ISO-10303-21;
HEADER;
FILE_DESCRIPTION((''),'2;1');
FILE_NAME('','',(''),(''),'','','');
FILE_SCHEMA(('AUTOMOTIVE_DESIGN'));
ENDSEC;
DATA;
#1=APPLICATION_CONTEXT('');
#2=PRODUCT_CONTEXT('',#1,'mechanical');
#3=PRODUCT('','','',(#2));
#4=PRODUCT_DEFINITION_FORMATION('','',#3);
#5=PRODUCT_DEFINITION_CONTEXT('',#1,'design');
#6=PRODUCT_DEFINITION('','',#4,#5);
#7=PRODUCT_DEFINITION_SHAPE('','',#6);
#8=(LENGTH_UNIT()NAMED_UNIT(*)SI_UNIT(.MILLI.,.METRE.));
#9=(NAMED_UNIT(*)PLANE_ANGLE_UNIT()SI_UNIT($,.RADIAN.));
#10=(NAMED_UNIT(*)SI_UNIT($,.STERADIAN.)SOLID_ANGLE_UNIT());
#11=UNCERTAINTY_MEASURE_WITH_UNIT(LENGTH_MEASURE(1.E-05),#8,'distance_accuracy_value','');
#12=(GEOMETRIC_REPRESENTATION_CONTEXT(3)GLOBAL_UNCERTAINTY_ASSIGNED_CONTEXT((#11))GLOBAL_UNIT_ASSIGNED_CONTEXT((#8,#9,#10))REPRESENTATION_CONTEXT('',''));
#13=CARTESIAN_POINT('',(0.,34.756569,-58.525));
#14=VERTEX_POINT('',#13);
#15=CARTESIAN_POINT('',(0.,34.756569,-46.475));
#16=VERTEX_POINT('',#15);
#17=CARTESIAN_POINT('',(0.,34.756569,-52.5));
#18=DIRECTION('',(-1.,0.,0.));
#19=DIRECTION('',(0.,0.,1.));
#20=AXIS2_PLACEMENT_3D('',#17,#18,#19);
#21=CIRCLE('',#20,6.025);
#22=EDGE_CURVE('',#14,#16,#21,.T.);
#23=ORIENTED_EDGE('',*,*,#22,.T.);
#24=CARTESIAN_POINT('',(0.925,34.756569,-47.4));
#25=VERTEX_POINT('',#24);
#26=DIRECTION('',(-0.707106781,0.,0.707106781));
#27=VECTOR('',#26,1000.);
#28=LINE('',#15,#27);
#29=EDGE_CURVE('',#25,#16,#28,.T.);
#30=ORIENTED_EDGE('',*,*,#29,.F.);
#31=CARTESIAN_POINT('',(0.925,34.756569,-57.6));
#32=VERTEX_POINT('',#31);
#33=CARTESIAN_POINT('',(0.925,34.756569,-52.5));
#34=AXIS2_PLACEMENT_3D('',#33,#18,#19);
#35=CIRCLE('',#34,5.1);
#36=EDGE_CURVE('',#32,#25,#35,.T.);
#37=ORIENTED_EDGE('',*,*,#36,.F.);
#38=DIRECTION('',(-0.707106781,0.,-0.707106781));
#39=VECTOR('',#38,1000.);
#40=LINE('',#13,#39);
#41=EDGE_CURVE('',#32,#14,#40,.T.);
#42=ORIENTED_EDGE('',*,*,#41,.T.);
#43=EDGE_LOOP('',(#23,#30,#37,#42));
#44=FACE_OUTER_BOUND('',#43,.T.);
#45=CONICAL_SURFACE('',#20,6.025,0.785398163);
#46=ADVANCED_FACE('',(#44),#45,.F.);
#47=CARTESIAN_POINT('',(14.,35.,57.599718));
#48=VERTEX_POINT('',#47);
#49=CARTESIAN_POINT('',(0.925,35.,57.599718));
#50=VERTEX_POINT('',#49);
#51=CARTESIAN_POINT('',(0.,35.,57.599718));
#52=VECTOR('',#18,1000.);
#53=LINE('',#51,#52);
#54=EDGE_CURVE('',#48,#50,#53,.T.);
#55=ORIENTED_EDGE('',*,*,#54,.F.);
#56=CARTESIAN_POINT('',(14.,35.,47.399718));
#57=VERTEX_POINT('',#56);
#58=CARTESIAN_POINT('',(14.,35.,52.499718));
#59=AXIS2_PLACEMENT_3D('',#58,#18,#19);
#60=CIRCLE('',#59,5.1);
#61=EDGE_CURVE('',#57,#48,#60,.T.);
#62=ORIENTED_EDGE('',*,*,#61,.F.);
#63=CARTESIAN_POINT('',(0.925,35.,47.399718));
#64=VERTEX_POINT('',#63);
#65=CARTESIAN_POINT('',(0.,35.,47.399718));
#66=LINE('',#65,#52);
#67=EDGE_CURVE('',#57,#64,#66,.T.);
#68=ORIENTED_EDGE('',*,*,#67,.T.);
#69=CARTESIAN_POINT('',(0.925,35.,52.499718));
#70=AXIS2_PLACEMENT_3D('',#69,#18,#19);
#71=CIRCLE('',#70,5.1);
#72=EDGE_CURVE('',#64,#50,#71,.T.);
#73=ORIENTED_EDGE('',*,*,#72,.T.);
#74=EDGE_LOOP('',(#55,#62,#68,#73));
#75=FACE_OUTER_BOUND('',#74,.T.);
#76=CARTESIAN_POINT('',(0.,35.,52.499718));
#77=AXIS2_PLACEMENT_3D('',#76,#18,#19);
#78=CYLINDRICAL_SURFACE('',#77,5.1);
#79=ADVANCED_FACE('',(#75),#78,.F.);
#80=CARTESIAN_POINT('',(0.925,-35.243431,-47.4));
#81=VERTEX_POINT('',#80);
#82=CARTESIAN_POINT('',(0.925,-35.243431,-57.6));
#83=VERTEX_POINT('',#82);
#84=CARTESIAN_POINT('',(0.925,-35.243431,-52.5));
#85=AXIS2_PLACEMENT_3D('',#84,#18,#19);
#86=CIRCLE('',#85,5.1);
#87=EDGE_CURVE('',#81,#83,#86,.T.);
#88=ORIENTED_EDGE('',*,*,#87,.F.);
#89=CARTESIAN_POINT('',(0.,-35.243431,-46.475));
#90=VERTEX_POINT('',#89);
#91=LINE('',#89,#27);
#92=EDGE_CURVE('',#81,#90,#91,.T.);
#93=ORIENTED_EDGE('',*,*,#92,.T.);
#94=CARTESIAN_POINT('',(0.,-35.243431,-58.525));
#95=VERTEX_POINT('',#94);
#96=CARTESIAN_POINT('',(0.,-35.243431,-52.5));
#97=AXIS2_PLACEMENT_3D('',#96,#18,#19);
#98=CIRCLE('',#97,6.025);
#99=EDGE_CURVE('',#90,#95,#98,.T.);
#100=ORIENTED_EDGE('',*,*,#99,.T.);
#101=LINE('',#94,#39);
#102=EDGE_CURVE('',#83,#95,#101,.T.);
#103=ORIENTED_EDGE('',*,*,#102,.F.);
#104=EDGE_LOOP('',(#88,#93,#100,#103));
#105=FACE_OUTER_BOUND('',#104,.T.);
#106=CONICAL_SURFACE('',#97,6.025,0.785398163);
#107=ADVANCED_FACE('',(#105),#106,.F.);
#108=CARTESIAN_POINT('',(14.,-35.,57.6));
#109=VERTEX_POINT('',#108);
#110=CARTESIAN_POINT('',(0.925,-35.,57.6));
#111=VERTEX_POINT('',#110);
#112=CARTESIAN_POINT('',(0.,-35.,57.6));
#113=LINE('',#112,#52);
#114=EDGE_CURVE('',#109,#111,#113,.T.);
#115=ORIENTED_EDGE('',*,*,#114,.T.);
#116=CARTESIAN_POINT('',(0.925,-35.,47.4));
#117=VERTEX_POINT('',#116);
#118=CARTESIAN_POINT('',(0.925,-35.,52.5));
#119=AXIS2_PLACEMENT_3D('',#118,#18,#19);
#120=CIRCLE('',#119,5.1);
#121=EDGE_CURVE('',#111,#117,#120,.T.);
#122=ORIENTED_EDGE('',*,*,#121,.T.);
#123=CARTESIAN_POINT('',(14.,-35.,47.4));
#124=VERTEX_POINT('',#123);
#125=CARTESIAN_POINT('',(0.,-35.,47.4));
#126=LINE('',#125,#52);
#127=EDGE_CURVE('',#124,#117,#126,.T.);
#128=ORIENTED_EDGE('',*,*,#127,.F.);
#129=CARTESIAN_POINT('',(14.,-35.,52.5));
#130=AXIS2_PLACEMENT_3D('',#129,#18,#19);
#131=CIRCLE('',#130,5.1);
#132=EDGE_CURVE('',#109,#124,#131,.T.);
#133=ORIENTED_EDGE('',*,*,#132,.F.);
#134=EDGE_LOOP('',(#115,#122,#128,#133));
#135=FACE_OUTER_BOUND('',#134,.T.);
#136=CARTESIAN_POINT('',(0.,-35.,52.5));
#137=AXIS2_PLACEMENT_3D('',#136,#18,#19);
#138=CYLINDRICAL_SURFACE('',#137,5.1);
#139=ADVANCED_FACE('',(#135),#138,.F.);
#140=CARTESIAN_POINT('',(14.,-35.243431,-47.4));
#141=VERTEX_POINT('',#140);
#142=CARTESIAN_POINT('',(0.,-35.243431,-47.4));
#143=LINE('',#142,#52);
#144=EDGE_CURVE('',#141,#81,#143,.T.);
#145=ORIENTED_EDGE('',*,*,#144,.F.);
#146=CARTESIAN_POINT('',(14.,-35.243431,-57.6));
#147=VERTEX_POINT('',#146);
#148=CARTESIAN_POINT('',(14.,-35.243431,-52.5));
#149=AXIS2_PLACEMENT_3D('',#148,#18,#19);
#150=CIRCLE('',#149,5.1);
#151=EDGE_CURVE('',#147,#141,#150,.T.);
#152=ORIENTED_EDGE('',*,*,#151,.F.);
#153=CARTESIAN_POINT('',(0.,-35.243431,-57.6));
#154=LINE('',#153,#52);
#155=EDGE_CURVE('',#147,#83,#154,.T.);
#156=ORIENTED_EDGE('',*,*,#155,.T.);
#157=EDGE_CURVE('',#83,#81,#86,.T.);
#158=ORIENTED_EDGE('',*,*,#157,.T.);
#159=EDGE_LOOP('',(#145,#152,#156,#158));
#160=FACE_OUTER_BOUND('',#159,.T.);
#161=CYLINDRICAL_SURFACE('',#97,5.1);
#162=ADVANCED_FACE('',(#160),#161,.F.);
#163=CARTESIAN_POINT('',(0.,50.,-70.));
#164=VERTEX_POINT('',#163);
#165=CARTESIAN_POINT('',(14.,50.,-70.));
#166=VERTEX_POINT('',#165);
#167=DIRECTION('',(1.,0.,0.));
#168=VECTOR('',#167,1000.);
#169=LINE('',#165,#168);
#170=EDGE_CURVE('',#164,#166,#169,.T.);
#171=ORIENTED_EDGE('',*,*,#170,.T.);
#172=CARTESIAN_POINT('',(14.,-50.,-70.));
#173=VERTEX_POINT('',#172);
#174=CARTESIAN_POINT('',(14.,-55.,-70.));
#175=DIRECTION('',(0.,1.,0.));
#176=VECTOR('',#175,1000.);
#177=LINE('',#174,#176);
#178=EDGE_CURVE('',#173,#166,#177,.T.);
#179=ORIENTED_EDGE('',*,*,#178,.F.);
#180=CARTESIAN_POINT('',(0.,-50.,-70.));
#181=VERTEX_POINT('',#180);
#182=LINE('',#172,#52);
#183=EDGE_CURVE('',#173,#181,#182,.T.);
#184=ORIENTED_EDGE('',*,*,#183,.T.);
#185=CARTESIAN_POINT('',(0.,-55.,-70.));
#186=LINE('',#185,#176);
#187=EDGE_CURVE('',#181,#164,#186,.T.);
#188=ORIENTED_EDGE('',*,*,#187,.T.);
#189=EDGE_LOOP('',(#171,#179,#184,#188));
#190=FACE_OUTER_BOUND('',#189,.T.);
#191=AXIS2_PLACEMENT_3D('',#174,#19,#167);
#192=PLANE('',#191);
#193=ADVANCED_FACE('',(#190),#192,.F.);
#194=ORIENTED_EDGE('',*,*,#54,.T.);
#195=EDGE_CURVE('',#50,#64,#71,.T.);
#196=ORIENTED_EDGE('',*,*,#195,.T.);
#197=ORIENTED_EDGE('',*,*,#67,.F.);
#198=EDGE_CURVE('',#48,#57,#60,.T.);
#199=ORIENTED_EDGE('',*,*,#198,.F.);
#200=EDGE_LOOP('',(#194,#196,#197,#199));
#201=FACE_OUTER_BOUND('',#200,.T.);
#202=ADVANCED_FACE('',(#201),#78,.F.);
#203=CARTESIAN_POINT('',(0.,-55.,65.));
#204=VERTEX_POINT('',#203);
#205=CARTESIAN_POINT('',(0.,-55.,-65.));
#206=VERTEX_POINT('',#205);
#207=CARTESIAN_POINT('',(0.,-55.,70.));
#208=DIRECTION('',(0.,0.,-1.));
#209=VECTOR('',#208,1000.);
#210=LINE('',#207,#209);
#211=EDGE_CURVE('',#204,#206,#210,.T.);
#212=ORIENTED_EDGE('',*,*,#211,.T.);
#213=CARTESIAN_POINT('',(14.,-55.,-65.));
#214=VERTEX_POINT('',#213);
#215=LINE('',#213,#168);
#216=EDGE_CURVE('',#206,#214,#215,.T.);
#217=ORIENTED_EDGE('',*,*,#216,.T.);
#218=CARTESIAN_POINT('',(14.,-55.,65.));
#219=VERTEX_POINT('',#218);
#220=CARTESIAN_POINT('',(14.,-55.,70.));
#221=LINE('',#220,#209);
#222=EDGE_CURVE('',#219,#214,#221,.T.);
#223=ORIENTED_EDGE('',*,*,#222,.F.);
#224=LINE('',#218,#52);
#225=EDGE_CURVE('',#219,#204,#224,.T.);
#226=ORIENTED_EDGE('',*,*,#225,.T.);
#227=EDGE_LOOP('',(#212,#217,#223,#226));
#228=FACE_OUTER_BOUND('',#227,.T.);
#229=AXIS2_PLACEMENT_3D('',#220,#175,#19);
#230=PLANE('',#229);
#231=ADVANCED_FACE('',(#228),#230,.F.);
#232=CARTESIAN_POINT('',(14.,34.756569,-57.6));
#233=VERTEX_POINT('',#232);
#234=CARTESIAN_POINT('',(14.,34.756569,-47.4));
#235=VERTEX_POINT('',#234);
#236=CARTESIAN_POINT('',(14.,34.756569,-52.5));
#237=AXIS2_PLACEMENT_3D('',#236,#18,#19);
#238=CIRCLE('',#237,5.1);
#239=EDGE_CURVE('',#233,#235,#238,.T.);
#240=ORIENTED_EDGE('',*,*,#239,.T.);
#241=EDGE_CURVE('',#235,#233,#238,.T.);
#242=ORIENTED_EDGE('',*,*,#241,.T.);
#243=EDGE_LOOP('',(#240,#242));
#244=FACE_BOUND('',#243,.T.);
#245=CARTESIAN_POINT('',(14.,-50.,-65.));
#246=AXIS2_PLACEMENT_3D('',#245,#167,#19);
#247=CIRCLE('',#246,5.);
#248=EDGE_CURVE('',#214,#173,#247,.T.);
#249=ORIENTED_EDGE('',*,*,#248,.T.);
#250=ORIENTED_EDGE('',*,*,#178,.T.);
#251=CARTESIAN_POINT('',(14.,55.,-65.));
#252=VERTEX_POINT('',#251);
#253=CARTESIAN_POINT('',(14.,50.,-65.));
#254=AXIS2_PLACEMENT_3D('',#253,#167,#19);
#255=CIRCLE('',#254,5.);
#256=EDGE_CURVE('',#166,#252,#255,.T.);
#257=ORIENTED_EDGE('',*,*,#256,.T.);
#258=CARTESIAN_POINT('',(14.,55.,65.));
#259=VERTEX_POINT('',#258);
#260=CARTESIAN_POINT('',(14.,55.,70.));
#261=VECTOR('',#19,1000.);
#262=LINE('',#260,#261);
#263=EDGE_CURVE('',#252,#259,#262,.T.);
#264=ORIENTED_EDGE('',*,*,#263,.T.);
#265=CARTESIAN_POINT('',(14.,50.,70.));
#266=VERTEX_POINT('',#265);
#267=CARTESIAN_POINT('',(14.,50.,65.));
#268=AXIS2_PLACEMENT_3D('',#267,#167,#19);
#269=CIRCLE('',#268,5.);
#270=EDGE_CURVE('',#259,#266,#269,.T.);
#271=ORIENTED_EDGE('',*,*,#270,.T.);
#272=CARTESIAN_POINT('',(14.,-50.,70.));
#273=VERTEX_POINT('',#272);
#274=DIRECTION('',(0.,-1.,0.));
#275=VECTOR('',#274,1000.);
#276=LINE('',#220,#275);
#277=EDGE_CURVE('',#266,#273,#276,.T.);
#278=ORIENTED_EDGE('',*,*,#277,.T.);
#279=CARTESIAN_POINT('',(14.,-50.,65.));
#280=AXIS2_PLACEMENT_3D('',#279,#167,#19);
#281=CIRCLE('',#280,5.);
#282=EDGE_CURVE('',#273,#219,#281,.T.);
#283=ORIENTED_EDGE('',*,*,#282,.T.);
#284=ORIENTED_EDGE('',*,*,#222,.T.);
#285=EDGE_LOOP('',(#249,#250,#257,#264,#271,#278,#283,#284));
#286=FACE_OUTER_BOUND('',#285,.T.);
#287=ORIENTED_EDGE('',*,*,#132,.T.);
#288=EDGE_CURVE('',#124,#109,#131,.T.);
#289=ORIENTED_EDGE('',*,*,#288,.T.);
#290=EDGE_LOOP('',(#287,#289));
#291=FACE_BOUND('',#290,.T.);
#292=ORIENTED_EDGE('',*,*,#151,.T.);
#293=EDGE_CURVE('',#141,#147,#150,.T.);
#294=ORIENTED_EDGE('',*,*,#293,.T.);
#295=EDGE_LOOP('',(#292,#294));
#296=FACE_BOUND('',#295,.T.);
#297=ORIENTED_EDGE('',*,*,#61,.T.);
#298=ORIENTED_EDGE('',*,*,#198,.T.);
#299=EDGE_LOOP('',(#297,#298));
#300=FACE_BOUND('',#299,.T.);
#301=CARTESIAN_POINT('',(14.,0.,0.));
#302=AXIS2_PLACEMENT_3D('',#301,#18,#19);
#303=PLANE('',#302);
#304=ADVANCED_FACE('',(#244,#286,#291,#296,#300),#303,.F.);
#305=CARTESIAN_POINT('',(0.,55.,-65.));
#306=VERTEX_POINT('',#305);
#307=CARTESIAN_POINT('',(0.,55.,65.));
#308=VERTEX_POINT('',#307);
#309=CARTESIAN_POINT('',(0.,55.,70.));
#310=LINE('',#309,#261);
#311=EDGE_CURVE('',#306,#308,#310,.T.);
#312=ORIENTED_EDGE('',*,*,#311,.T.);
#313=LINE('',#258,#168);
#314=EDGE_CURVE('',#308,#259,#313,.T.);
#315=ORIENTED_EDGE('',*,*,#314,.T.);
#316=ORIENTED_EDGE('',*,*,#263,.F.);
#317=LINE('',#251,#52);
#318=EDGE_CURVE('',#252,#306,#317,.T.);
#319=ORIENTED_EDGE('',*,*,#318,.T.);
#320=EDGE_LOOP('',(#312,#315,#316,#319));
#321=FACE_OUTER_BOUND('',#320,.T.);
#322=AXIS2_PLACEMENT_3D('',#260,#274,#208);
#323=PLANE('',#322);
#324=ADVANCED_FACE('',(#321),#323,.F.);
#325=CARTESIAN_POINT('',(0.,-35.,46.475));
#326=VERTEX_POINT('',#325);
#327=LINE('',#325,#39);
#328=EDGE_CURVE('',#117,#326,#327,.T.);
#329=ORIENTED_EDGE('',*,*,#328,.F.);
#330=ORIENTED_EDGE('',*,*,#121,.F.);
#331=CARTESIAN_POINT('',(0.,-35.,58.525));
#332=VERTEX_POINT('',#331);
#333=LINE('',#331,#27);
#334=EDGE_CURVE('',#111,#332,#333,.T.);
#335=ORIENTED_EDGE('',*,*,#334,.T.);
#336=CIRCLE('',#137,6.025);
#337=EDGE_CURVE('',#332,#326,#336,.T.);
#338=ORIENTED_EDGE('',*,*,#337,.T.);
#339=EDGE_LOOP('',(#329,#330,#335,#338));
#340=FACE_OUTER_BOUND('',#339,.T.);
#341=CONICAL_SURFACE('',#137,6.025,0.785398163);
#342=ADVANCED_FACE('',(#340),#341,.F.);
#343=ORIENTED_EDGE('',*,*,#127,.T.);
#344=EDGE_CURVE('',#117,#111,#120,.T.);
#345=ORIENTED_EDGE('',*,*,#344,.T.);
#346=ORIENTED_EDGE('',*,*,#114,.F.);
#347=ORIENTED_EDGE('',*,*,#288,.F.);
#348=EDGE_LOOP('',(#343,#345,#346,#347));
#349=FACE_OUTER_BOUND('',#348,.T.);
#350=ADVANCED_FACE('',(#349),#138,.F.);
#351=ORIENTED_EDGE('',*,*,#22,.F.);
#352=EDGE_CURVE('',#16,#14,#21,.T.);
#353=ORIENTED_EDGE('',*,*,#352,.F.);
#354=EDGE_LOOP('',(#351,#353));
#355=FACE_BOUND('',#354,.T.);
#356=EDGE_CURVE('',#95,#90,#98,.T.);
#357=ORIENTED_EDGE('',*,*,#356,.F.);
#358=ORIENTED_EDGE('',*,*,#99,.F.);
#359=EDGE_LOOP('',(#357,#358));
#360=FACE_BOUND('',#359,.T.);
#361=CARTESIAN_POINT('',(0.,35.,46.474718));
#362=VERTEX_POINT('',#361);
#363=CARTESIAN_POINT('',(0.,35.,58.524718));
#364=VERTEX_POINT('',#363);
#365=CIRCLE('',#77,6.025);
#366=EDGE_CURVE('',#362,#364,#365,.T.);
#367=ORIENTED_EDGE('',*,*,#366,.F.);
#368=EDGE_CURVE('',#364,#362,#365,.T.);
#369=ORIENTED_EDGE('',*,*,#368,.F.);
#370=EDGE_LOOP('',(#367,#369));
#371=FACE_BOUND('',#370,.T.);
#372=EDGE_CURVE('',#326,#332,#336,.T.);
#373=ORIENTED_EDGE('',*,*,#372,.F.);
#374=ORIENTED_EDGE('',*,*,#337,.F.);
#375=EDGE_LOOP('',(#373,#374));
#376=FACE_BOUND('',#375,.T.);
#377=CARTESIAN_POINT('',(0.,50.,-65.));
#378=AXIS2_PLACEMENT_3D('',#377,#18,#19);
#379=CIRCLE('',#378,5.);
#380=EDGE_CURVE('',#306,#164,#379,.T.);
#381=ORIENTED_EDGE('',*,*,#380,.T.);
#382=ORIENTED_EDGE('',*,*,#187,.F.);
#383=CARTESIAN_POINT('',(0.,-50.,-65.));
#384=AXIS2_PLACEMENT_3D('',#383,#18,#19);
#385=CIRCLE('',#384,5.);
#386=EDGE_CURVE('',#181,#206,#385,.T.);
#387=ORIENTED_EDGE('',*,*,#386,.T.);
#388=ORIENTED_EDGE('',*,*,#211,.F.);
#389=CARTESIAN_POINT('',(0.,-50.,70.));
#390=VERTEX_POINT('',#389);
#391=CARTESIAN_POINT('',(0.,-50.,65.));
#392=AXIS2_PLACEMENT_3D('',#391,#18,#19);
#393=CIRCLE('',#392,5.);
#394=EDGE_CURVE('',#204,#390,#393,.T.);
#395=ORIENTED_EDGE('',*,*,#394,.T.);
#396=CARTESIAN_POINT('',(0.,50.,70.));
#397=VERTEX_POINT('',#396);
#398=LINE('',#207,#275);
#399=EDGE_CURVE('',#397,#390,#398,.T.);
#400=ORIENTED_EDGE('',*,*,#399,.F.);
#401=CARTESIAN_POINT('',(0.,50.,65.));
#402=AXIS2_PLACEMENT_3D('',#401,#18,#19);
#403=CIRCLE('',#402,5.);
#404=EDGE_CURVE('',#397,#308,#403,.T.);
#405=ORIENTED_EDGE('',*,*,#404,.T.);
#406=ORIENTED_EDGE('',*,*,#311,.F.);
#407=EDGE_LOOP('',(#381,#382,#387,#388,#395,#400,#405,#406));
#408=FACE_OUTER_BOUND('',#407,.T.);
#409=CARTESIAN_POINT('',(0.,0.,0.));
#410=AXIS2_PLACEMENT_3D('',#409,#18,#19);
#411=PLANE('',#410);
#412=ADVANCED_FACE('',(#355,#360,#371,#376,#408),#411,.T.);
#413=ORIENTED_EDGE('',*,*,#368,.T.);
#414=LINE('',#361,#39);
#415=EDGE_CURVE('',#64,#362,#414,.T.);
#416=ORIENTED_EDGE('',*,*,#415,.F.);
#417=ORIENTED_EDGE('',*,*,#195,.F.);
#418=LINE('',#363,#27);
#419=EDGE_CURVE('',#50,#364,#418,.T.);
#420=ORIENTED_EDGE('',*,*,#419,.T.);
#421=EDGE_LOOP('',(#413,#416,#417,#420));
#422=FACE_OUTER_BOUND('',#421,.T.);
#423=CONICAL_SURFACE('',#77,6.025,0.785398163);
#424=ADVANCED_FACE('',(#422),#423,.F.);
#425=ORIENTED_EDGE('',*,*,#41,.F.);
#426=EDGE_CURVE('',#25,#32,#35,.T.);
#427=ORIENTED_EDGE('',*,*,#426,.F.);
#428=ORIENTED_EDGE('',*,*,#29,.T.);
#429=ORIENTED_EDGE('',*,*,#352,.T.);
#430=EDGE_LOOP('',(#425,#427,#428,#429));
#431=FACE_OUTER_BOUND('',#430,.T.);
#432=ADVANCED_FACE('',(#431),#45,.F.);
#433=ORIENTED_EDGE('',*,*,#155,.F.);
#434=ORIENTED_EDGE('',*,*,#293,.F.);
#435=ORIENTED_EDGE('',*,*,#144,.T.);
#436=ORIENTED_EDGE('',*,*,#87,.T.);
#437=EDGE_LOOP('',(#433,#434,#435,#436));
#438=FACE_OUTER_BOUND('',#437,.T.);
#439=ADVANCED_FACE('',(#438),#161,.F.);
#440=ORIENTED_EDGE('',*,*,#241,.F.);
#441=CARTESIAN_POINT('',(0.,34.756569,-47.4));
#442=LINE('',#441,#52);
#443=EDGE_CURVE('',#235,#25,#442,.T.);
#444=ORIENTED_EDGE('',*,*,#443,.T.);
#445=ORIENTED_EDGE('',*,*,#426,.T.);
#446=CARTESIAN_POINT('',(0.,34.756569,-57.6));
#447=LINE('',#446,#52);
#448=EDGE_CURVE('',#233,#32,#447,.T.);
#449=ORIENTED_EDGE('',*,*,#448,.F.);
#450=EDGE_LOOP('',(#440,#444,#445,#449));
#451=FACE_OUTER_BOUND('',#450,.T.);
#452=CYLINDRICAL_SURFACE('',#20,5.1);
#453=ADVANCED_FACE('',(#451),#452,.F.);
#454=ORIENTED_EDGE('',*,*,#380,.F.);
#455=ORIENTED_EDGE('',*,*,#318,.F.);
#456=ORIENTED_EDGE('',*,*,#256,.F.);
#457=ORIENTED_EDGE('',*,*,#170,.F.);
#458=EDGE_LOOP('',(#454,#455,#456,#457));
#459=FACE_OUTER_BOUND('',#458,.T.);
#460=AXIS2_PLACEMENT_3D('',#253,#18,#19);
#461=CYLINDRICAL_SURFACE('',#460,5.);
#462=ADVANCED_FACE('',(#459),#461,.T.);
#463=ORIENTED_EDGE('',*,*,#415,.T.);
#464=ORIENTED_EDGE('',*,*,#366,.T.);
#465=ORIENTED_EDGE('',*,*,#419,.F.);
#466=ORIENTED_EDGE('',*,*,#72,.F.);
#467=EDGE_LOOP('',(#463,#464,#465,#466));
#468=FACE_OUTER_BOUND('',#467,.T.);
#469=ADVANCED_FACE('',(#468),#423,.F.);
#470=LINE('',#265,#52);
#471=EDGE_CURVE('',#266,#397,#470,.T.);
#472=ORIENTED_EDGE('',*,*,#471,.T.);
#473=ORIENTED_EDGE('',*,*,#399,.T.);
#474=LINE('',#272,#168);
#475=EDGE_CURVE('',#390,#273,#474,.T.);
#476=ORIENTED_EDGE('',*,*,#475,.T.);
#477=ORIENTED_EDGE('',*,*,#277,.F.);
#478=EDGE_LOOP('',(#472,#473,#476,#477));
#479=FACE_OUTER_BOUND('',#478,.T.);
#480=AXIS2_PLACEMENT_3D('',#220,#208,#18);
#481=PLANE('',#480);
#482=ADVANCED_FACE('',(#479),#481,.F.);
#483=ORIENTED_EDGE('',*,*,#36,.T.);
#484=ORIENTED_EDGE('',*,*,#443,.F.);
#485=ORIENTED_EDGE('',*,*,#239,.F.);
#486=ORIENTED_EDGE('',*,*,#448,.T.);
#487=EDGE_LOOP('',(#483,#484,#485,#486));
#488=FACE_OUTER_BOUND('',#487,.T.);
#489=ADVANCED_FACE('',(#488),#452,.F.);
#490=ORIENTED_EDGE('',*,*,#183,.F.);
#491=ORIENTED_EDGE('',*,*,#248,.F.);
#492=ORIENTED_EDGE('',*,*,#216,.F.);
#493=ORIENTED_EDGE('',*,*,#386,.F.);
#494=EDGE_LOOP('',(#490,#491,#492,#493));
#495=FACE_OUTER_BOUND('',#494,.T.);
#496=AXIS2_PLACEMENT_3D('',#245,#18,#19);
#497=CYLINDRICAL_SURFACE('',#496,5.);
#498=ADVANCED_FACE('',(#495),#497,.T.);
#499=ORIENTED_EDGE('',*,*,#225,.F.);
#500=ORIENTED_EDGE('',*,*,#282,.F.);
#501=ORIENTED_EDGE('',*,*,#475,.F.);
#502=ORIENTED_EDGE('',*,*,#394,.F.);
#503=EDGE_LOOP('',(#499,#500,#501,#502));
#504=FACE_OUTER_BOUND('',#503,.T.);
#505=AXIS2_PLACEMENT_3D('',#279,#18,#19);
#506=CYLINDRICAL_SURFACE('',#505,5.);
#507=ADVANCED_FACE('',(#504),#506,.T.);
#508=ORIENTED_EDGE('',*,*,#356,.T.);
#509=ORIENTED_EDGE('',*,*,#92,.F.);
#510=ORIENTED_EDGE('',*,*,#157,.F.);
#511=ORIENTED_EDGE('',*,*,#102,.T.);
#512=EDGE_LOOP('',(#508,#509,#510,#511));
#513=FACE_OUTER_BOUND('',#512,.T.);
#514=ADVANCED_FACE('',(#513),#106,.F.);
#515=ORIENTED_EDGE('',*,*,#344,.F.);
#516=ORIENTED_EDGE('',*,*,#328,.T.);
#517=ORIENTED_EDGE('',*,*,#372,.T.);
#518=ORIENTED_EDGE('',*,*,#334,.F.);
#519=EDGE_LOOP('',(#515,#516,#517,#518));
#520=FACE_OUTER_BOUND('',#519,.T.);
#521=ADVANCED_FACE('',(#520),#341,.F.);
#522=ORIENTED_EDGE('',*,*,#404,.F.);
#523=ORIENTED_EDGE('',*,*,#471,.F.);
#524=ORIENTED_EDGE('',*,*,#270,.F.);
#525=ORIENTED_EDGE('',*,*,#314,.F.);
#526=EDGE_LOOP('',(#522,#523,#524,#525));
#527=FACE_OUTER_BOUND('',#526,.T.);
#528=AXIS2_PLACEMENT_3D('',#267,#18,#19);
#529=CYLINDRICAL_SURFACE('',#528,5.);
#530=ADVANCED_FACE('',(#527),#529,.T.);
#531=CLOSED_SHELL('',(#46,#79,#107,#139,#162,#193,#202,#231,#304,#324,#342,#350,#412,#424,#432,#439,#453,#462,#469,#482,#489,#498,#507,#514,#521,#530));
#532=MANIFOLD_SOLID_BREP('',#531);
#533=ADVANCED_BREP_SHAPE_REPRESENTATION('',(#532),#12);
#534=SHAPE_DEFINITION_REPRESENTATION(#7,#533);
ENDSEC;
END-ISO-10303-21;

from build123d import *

# Parameters (mm, degrees)
SKETCH1_W                    = 140
SKETCH1_H                    = 110
BOSS_EXTRUDE1_DEPTH          = 14
FILLET1_R                    = 5
M12_TAPPED_HOLE1_D           = 10.2
M12_TAPPED_HOLE1_DEPTH       = 32.75
M12_TAPPED_HOLE1_CSINK_D     = 12.05
M12_TAPPED_HOLE1_CSINK_ANGLE = 90
M12_TAPPED_HOLE1_TIP         = 3.064389157


with BuildPart() as part:
    # Sketch1 → Boss-Extrude1 (new body)
    with BuildSketch(Plane(origin=(0, 0, 0), x_dir=(0, 0, -1), z_dir=(1, 0, 0))):
        Rectangle(SKETCH1_W, SKETCH1_H)
    extrude(amount=BOSS_EXTRUDE1_DEPTH)

    # Fillet1
    fillet1_edges = [part.edges().sort_by_distance(p)[0] for p in [
        (7, -55, -70),
        (7, -55, 70),
        (7, 55, 70),
        (7, 55, -70),
    ]]
    fillet(fillet1_edges, radius=FILLET1_R)

    # M12 Tapped Hole1
    with Locations(Plane.ZY):
        with Locations((-52.5, 34.756569307), (52.499717816, 35), (52.5, -35), (-52.5, -35.243430693)):
            CounterSinkHole(M12_TAPPED_HOLE1_D / 2, M12_TAPPED_HOLE1_CSINK_D / 2, depth=M12_TAPPED_HOLE1_DEPTH, counter_sink_angle=M12_TAPPED_HOLE1_CSINK_ANGLE)
            with Locations((0, 0, -(M12_TAPPED_HOLE1_DEPTH + M12_TAPPED_HOLE1_TIP / 2))):  # 118° drill point
                Cone(0, M12_TAPPED_HOLE1_D / 2, M12_TAPPED_HOLE1_TIP, mode=Mode.SUBTRACT)


solid = part.part
